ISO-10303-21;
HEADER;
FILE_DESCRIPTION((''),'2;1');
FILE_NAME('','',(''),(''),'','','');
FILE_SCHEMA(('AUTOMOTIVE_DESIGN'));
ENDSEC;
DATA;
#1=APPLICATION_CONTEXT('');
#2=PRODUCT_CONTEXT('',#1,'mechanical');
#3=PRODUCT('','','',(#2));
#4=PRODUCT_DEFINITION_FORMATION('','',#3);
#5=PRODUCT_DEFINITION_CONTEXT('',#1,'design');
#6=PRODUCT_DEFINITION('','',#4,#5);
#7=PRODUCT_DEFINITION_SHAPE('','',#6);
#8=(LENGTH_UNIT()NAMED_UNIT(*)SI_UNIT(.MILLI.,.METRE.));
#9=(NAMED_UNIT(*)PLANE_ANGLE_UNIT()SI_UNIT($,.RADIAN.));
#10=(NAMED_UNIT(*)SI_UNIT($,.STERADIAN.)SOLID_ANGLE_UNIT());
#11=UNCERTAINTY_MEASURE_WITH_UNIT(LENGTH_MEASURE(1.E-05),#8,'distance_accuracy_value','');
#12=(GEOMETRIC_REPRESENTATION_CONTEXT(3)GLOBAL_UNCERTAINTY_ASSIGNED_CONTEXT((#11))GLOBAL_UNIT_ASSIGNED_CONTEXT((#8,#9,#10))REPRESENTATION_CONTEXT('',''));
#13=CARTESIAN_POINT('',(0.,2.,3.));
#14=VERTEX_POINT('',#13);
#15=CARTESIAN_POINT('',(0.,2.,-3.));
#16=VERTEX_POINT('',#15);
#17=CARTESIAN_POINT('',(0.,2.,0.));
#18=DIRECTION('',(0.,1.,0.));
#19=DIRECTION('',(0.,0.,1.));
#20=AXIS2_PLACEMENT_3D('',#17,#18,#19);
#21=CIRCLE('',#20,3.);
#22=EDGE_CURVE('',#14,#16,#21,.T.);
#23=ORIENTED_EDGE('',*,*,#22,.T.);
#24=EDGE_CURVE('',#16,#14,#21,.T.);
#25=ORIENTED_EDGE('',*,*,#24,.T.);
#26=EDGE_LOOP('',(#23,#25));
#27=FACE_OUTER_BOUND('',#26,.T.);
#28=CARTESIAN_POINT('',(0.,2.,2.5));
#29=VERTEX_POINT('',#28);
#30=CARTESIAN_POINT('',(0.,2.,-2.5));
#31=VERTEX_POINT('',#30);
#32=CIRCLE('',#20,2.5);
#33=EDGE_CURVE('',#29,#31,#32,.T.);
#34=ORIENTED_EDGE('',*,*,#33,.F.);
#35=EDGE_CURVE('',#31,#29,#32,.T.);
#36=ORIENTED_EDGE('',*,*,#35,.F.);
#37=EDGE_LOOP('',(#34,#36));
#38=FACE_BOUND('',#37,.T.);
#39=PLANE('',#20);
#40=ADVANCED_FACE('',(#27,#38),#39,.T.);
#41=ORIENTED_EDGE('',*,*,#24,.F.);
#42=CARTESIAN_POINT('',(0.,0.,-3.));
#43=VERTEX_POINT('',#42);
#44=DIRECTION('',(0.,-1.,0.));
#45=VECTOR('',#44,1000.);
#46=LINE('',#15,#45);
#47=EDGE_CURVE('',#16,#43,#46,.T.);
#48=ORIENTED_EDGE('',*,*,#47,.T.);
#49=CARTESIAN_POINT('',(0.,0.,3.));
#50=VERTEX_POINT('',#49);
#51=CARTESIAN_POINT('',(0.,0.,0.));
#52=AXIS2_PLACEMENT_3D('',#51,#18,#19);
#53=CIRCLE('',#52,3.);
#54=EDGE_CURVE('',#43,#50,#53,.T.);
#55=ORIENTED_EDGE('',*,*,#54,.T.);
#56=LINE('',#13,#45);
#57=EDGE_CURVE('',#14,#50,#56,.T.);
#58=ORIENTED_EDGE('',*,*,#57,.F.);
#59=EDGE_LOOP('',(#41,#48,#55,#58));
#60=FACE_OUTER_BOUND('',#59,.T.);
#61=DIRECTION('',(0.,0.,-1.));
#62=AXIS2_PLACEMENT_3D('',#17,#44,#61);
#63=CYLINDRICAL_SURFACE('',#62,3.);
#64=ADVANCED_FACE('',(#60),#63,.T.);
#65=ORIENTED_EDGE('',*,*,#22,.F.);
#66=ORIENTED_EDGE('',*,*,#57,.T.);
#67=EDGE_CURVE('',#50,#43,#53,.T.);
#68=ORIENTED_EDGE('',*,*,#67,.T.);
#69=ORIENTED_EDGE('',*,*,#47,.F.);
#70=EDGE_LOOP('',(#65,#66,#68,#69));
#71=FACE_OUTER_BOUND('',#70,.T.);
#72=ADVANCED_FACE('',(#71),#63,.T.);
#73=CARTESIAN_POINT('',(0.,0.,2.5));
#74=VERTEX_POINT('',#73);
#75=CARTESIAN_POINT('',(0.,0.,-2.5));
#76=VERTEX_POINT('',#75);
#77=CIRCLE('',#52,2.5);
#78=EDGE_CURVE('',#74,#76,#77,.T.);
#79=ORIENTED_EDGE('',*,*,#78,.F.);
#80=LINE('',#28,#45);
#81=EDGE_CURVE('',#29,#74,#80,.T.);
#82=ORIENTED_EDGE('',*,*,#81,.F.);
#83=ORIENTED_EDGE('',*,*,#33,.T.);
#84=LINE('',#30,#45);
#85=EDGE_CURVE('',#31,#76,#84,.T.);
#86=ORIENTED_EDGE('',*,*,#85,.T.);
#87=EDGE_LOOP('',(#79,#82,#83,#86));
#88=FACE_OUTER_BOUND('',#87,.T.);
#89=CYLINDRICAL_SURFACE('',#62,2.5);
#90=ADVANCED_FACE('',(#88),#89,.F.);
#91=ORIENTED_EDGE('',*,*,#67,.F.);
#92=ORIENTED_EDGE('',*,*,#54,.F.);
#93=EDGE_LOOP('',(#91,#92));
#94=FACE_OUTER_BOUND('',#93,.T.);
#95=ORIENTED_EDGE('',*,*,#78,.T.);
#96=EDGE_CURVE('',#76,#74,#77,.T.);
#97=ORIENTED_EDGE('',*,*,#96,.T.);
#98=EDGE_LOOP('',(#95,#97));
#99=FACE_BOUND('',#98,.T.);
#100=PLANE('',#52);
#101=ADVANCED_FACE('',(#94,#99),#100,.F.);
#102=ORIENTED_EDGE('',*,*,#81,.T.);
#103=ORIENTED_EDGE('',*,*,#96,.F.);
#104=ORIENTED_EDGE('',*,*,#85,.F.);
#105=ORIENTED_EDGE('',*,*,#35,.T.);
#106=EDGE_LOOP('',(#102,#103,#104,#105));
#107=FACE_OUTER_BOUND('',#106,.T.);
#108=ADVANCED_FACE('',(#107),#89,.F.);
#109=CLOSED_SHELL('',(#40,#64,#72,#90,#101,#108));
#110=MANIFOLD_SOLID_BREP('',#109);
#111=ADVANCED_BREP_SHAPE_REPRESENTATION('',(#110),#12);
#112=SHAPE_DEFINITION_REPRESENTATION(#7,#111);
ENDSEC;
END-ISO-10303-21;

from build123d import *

# Parameters (mm, degrees)
SKETCH1_R           = 3
SKETCH1_R_2         = 2.5
BOSS_EXTRUDE1_DEPTH = 2


with BuildPart() as part:
    # Sketch1 → Boss-Extrude1 (new body)
    with BuildSketch(Plane(origin=(0, 0, 0), x_dir=(1, 0, 0), z_dir=(0, 1, 0))):
        with Locations(Location((0, 0, 0), (0, 0, 270))):
            Circle(SKETCH1_R)
        with Locations(Location((0, 0, 0), (0, 0, 270))):
            Circle(SKETCH1_R_2, mode=Mode.SUBTRACT)
    extrude(amount=BOSS_EXTRUDE1_DEPTH)


solid = part.part
